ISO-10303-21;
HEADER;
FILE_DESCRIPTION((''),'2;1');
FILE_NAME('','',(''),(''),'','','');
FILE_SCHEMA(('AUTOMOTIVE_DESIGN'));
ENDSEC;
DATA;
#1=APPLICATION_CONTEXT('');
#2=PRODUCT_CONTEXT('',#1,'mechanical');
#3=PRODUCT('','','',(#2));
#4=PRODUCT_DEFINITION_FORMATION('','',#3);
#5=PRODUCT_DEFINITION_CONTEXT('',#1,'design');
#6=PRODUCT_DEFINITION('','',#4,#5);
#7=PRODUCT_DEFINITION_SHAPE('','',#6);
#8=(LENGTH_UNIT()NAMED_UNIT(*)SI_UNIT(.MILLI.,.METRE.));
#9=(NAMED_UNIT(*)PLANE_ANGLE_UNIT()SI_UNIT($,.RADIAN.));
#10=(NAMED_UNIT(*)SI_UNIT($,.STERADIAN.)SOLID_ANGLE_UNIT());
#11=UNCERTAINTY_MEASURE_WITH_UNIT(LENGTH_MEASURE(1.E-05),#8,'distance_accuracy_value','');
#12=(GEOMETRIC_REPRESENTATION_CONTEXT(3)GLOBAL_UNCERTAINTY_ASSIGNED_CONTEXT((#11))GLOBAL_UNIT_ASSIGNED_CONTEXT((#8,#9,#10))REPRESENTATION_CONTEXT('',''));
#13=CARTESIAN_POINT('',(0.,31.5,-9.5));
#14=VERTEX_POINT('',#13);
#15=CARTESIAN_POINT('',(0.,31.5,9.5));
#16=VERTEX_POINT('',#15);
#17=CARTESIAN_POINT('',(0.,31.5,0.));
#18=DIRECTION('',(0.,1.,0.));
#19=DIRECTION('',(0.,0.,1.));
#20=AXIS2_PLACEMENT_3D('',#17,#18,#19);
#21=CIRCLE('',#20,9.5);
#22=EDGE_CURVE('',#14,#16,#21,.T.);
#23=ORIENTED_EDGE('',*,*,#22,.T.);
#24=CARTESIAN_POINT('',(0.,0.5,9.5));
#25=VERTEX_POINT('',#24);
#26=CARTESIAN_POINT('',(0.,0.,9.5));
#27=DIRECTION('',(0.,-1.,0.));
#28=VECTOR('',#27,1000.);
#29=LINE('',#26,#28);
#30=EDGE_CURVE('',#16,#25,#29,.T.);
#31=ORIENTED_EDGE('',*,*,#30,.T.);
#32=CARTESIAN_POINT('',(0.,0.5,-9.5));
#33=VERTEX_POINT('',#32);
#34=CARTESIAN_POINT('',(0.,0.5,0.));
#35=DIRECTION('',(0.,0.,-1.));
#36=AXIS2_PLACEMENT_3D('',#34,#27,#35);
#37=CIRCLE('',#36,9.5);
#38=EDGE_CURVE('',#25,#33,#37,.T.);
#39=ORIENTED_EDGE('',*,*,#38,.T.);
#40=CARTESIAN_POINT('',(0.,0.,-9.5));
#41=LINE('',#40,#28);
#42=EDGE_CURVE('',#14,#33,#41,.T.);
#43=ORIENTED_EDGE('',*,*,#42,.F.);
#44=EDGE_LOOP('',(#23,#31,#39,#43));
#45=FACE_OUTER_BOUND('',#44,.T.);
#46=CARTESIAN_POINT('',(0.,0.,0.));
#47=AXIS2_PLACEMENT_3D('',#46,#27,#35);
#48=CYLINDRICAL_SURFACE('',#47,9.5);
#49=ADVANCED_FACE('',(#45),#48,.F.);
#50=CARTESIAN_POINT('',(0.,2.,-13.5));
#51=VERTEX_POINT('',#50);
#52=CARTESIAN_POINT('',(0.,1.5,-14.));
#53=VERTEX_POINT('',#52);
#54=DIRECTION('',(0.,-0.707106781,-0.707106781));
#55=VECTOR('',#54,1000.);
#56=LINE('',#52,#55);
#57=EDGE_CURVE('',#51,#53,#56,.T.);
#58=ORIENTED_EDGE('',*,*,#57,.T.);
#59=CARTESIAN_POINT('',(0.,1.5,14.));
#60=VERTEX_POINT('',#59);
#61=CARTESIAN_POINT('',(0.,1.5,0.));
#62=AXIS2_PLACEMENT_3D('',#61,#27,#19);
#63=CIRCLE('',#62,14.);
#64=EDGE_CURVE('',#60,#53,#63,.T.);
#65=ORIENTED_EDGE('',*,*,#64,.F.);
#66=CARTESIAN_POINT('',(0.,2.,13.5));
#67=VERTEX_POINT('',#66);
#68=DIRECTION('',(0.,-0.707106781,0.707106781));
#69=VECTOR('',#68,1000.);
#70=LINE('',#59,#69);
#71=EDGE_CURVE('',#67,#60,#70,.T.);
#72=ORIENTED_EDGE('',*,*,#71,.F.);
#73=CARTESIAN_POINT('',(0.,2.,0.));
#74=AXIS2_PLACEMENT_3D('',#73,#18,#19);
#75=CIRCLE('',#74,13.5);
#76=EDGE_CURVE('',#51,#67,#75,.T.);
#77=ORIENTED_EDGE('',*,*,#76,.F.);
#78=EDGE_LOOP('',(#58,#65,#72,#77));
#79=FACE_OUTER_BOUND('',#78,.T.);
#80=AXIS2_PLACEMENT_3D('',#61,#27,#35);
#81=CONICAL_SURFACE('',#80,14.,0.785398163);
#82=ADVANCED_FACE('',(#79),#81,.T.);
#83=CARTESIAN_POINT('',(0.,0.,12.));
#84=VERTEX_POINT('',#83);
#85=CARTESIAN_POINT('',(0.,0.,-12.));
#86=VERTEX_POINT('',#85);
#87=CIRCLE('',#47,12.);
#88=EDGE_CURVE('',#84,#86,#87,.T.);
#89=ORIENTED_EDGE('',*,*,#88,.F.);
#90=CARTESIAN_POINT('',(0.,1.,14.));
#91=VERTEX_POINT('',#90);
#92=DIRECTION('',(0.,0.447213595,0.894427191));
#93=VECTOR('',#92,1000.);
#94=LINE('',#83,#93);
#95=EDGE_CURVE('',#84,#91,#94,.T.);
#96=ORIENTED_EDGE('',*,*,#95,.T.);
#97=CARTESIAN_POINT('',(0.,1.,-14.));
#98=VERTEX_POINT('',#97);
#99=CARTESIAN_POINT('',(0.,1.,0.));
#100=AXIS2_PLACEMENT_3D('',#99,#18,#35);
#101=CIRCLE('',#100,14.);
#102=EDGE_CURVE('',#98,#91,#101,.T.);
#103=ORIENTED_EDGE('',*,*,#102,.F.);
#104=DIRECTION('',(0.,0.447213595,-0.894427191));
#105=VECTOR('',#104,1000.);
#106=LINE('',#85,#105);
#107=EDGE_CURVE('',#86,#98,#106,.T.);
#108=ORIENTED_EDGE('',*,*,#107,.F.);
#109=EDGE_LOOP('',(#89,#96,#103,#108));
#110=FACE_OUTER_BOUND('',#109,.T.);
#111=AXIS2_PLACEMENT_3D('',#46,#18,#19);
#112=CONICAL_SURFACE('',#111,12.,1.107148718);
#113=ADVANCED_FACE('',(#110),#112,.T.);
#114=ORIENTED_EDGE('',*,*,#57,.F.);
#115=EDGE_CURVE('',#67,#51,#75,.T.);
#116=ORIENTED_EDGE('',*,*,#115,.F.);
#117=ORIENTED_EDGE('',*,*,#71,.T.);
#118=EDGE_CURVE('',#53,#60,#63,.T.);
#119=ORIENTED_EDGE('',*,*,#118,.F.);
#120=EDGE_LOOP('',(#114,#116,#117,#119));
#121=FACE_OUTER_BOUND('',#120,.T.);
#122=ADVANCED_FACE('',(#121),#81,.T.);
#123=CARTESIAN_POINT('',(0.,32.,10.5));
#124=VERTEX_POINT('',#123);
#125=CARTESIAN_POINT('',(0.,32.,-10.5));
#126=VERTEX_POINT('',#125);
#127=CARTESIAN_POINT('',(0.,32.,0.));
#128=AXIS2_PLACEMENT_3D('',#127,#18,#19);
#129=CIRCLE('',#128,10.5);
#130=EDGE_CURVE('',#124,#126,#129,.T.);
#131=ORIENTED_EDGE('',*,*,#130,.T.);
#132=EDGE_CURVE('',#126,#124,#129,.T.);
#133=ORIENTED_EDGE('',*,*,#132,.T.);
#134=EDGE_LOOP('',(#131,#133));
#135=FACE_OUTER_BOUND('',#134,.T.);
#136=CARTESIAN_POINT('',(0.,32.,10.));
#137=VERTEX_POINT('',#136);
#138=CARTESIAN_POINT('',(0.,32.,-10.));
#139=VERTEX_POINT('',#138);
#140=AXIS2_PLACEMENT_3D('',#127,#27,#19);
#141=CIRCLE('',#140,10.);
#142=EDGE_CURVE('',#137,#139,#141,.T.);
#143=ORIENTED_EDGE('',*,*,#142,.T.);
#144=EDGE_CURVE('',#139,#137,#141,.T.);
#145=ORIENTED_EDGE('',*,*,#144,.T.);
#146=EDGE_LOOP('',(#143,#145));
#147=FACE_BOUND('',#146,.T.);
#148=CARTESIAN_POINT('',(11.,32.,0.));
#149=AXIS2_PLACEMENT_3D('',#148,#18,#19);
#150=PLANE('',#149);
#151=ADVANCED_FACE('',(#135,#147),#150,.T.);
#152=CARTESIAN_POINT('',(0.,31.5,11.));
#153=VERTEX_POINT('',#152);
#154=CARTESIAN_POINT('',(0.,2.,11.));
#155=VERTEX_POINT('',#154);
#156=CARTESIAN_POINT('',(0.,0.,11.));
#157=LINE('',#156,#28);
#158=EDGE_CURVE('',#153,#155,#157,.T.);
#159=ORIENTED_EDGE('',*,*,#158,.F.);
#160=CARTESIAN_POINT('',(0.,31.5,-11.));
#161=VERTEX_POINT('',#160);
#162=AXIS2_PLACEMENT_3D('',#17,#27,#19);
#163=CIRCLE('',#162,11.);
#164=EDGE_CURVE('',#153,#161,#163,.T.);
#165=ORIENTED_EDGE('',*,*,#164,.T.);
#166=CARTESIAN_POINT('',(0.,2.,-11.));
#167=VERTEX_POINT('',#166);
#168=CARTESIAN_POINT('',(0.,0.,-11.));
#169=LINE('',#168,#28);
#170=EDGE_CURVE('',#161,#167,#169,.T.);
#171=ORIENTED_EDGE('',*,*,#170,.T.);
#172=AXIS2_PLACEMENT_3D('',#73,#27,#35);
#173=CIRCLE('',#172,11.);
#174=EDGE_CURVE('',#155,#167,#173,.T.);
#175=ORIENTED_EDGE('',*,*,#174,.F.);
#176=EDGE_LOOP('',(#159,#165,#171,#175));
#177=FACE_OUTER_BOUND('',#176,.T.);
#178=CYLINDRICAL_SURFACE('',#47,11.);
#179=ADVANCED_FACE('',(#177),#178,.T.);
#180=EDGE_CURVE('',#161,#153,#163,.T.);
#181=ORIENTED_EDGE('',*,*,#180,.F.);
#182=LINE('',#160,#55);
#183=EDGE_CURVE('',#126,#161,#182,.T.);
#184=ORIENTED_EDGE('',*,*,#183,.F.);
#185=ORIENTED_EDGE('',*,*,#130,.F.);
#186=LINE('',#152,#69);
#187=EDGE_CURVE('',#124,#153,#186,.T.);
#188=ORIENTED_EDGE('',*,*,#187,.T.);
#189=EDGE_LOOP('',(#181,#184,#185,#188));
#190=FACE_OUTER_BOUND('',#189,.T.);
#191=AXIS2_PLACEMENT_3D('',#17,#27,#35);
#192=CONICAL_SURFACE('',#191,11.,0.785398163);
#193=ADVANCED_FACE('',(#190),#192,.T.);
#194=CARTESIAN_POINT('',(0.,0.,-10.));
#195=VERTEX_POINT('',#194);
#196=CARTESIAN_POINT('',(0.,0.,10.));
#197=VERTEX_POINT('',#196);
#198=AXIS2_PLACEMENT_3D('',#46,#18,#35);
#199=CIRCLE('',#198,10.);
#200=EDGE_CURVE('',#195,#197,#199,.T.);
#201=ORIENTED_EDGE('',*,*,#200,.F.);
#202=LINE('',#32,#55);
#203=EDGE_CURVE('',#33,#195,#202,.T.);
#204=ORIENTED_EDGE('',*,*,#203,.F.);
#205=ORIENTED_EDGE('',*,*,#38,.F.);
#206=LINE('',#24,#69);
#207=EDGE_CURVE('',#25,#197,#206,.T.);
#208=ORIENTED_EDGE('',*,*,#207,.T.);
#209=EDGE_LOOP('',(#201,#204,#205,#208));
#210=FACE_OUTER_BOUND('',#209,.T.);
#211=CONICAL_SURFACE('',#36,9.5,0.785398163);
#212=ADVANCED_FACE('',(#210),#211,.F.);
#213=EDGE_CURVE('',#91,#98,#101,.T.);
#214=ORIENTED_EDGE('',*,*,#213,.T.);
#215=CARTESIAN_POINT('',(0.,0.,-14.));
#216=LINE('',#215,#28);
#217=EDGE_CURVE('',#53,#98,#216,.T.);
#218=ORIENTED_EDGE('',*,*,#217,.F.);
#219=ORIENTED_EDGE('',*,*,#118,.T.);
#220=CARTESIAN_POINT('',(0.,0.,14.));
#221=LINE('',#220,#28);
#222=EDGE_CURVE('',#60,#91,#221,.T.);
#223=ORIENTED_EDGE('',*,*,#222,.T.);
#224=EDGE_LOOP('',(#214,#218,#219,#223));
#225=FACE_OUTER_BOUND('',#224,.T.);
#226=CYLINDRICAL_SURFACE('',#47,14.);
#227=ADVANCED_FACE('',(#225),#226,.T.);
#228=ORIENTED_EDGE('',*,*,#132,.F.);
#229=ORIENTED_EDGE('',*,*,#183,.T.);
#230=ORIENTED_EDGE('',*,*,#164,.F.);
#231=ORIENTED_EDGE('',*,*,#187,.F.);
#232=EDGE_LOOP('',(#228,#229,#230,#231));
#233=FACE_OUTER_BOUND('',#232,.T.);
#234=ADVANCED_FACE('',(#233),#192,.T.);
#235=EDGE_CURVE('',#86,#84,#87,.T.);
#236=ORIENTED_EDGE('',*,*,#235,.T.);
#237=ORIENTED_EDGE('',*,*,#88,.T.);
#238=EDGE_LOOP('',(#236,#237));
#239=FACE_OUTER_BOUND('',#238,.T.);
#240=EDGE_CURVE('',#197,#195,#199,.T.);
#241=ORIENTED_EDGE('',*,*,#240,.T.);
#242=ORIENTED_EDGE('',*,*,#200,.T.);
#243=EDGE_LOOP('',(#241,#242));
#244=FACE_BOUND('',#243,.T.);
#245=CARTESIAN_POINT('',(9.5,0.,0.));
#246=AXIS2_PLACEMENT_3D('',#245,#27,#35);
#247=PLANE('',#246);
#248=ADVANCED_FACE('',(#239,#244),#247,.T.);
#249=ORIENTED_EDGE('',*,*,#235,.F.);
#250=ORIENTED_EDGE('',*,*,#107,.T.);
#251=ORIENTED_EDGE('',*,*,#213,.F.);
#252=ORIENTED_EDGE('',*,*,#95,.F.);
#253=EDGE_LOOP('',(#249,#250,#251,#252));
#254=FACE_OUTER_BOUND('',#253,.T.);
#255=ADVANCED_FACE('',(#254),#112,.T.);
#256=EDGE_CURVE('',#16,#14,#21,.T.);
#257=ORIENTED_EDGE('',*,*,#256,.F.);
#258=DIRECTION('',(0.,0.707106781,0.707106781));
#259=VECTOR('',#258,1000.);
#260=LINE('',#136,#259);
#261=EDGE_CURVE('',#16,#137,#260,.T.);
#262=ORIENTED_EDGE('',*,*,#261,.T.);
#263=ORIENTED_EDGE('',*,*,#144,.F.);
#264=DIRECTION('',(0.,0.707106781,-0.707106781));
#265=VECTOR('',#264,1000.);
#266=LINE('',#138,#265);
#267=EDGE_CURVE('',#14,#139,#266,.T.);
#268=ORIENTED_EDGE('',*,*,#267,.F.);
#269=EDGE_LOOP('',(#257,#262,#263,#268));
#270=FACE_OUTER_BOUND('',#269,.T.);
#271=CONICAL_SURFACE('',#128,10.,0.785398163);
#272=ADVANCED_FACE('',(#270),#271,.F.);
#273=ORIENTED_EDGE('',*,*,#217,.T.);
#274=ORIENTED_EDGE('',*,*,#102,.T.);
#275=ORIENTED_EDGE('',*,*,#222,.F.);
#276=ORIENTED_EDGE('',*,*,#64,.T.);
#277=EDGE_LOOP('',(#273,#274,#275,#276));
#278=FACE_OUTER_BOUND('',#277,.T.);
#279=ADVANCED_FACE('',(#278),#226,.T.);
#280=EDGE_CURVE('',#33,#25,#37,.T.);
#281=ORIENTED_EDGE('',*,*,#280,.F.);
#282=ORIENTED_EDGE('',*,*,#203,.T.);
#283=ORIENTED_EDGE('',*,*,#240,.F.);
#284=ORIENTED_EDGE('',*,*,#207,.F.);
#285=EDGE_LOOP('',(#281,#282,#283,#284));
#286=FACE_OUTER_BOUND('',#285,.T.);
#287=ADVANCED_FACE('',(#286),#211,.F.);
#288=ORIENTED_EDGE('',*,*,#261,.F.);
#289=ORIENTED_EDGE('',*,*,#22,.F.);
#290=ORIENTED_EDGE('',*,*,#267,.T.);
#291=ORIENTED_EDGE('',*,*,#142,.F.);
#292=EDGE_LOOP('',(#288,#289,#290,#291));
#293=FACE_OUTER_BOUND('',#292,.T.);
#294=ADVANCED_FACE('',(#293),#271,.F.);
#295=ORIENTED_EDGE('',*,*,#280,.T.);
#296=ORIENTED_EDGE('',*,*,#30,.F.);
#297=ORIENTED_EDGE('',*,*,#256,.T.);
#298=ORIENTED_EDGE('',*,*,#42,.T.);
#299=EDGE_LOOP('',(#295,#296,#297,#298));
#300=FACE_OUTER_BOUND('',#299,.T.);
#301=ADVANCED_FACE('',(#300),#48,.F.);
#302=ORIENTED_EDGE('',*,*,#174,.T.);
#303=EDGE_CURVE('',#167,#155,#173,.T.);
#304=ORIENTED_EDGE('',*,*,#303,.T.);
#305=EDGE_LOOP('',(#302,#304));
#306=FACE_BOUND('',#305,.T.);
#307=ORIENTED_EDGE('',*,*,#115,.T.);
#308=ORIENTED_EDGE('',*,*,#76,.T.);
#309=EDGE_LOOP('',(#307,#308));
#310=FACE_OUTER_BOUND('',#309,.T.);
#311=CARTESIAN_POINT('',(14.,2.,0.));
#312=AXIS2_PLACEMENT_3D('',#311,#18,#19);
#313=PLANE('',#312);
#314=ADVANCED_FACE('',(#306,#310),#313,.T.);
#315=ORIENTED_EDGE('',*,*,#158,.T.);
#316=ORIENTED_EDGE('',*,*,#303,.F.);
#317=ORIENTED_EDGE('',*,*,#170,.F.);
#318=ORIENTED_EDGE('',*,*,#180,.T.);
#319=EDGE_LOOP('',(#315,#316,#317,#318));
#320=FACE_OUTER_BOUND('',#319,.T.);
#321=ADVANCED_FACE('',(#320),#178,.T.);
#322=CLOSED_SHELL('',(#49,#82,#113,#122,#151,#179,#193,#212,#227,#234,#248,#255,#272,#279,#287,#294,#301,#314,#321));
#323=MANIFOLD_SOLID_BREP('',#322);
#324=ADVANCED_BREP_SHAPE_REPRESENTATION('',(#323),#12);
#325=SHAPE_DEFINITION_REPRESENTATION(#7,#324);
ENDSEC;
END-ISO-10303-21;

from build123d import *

# Parameters (mm, degrees)
CHAMFER1_SIZE  = 0.5
CHAMFER2_SIZE  = 1
CHAMFER2_SIZE2 = 2


with BuildPart() as part:
    # Sketch1 → Revolve1 (revolve)
    with BuildSketch(Plane.XY, mode=Mode.PRIVATE) as revolve1_sk:
        Polygon((9.5, 0), (14, 0), (14, 2), (11, 2), (11, 32), (9.5, 32), align=None)
    revolve(revolve1_sk.sketch.rotate(Axis((0, 0, 0), (0, 1, 0)), 90), axis=Axis((0, 0, 0), (0, 1, 0)))

    # Chamfer1
    chamfer1_edges = [part.edges().sort_by_distance(p)[0] for p in [
        (0, 32, 9.5),
        (0, 32, 11),
        (0, 2, 14),
        (0, 0, 9.5),
    ]]
    chamfer(chamfer1_edges, length=CHAMFER1_SIZE)

    # Chamfer2
    chamfer2_edges = [part.edges().sort_by_distance(p)[0] for p in [
        (0, 0, 14),
    ]]
    chamfer2_side = [part.faces().sort_by_distance(p)[0] for p in [
        (0, 0.75, 14),
    ]]
    chamfer(chamfer2_edges, length=CHAMFER2_SIZE, length2=CHAMFER2_SIZE2, reference=chamfer2_side[0])


solid = part.part
